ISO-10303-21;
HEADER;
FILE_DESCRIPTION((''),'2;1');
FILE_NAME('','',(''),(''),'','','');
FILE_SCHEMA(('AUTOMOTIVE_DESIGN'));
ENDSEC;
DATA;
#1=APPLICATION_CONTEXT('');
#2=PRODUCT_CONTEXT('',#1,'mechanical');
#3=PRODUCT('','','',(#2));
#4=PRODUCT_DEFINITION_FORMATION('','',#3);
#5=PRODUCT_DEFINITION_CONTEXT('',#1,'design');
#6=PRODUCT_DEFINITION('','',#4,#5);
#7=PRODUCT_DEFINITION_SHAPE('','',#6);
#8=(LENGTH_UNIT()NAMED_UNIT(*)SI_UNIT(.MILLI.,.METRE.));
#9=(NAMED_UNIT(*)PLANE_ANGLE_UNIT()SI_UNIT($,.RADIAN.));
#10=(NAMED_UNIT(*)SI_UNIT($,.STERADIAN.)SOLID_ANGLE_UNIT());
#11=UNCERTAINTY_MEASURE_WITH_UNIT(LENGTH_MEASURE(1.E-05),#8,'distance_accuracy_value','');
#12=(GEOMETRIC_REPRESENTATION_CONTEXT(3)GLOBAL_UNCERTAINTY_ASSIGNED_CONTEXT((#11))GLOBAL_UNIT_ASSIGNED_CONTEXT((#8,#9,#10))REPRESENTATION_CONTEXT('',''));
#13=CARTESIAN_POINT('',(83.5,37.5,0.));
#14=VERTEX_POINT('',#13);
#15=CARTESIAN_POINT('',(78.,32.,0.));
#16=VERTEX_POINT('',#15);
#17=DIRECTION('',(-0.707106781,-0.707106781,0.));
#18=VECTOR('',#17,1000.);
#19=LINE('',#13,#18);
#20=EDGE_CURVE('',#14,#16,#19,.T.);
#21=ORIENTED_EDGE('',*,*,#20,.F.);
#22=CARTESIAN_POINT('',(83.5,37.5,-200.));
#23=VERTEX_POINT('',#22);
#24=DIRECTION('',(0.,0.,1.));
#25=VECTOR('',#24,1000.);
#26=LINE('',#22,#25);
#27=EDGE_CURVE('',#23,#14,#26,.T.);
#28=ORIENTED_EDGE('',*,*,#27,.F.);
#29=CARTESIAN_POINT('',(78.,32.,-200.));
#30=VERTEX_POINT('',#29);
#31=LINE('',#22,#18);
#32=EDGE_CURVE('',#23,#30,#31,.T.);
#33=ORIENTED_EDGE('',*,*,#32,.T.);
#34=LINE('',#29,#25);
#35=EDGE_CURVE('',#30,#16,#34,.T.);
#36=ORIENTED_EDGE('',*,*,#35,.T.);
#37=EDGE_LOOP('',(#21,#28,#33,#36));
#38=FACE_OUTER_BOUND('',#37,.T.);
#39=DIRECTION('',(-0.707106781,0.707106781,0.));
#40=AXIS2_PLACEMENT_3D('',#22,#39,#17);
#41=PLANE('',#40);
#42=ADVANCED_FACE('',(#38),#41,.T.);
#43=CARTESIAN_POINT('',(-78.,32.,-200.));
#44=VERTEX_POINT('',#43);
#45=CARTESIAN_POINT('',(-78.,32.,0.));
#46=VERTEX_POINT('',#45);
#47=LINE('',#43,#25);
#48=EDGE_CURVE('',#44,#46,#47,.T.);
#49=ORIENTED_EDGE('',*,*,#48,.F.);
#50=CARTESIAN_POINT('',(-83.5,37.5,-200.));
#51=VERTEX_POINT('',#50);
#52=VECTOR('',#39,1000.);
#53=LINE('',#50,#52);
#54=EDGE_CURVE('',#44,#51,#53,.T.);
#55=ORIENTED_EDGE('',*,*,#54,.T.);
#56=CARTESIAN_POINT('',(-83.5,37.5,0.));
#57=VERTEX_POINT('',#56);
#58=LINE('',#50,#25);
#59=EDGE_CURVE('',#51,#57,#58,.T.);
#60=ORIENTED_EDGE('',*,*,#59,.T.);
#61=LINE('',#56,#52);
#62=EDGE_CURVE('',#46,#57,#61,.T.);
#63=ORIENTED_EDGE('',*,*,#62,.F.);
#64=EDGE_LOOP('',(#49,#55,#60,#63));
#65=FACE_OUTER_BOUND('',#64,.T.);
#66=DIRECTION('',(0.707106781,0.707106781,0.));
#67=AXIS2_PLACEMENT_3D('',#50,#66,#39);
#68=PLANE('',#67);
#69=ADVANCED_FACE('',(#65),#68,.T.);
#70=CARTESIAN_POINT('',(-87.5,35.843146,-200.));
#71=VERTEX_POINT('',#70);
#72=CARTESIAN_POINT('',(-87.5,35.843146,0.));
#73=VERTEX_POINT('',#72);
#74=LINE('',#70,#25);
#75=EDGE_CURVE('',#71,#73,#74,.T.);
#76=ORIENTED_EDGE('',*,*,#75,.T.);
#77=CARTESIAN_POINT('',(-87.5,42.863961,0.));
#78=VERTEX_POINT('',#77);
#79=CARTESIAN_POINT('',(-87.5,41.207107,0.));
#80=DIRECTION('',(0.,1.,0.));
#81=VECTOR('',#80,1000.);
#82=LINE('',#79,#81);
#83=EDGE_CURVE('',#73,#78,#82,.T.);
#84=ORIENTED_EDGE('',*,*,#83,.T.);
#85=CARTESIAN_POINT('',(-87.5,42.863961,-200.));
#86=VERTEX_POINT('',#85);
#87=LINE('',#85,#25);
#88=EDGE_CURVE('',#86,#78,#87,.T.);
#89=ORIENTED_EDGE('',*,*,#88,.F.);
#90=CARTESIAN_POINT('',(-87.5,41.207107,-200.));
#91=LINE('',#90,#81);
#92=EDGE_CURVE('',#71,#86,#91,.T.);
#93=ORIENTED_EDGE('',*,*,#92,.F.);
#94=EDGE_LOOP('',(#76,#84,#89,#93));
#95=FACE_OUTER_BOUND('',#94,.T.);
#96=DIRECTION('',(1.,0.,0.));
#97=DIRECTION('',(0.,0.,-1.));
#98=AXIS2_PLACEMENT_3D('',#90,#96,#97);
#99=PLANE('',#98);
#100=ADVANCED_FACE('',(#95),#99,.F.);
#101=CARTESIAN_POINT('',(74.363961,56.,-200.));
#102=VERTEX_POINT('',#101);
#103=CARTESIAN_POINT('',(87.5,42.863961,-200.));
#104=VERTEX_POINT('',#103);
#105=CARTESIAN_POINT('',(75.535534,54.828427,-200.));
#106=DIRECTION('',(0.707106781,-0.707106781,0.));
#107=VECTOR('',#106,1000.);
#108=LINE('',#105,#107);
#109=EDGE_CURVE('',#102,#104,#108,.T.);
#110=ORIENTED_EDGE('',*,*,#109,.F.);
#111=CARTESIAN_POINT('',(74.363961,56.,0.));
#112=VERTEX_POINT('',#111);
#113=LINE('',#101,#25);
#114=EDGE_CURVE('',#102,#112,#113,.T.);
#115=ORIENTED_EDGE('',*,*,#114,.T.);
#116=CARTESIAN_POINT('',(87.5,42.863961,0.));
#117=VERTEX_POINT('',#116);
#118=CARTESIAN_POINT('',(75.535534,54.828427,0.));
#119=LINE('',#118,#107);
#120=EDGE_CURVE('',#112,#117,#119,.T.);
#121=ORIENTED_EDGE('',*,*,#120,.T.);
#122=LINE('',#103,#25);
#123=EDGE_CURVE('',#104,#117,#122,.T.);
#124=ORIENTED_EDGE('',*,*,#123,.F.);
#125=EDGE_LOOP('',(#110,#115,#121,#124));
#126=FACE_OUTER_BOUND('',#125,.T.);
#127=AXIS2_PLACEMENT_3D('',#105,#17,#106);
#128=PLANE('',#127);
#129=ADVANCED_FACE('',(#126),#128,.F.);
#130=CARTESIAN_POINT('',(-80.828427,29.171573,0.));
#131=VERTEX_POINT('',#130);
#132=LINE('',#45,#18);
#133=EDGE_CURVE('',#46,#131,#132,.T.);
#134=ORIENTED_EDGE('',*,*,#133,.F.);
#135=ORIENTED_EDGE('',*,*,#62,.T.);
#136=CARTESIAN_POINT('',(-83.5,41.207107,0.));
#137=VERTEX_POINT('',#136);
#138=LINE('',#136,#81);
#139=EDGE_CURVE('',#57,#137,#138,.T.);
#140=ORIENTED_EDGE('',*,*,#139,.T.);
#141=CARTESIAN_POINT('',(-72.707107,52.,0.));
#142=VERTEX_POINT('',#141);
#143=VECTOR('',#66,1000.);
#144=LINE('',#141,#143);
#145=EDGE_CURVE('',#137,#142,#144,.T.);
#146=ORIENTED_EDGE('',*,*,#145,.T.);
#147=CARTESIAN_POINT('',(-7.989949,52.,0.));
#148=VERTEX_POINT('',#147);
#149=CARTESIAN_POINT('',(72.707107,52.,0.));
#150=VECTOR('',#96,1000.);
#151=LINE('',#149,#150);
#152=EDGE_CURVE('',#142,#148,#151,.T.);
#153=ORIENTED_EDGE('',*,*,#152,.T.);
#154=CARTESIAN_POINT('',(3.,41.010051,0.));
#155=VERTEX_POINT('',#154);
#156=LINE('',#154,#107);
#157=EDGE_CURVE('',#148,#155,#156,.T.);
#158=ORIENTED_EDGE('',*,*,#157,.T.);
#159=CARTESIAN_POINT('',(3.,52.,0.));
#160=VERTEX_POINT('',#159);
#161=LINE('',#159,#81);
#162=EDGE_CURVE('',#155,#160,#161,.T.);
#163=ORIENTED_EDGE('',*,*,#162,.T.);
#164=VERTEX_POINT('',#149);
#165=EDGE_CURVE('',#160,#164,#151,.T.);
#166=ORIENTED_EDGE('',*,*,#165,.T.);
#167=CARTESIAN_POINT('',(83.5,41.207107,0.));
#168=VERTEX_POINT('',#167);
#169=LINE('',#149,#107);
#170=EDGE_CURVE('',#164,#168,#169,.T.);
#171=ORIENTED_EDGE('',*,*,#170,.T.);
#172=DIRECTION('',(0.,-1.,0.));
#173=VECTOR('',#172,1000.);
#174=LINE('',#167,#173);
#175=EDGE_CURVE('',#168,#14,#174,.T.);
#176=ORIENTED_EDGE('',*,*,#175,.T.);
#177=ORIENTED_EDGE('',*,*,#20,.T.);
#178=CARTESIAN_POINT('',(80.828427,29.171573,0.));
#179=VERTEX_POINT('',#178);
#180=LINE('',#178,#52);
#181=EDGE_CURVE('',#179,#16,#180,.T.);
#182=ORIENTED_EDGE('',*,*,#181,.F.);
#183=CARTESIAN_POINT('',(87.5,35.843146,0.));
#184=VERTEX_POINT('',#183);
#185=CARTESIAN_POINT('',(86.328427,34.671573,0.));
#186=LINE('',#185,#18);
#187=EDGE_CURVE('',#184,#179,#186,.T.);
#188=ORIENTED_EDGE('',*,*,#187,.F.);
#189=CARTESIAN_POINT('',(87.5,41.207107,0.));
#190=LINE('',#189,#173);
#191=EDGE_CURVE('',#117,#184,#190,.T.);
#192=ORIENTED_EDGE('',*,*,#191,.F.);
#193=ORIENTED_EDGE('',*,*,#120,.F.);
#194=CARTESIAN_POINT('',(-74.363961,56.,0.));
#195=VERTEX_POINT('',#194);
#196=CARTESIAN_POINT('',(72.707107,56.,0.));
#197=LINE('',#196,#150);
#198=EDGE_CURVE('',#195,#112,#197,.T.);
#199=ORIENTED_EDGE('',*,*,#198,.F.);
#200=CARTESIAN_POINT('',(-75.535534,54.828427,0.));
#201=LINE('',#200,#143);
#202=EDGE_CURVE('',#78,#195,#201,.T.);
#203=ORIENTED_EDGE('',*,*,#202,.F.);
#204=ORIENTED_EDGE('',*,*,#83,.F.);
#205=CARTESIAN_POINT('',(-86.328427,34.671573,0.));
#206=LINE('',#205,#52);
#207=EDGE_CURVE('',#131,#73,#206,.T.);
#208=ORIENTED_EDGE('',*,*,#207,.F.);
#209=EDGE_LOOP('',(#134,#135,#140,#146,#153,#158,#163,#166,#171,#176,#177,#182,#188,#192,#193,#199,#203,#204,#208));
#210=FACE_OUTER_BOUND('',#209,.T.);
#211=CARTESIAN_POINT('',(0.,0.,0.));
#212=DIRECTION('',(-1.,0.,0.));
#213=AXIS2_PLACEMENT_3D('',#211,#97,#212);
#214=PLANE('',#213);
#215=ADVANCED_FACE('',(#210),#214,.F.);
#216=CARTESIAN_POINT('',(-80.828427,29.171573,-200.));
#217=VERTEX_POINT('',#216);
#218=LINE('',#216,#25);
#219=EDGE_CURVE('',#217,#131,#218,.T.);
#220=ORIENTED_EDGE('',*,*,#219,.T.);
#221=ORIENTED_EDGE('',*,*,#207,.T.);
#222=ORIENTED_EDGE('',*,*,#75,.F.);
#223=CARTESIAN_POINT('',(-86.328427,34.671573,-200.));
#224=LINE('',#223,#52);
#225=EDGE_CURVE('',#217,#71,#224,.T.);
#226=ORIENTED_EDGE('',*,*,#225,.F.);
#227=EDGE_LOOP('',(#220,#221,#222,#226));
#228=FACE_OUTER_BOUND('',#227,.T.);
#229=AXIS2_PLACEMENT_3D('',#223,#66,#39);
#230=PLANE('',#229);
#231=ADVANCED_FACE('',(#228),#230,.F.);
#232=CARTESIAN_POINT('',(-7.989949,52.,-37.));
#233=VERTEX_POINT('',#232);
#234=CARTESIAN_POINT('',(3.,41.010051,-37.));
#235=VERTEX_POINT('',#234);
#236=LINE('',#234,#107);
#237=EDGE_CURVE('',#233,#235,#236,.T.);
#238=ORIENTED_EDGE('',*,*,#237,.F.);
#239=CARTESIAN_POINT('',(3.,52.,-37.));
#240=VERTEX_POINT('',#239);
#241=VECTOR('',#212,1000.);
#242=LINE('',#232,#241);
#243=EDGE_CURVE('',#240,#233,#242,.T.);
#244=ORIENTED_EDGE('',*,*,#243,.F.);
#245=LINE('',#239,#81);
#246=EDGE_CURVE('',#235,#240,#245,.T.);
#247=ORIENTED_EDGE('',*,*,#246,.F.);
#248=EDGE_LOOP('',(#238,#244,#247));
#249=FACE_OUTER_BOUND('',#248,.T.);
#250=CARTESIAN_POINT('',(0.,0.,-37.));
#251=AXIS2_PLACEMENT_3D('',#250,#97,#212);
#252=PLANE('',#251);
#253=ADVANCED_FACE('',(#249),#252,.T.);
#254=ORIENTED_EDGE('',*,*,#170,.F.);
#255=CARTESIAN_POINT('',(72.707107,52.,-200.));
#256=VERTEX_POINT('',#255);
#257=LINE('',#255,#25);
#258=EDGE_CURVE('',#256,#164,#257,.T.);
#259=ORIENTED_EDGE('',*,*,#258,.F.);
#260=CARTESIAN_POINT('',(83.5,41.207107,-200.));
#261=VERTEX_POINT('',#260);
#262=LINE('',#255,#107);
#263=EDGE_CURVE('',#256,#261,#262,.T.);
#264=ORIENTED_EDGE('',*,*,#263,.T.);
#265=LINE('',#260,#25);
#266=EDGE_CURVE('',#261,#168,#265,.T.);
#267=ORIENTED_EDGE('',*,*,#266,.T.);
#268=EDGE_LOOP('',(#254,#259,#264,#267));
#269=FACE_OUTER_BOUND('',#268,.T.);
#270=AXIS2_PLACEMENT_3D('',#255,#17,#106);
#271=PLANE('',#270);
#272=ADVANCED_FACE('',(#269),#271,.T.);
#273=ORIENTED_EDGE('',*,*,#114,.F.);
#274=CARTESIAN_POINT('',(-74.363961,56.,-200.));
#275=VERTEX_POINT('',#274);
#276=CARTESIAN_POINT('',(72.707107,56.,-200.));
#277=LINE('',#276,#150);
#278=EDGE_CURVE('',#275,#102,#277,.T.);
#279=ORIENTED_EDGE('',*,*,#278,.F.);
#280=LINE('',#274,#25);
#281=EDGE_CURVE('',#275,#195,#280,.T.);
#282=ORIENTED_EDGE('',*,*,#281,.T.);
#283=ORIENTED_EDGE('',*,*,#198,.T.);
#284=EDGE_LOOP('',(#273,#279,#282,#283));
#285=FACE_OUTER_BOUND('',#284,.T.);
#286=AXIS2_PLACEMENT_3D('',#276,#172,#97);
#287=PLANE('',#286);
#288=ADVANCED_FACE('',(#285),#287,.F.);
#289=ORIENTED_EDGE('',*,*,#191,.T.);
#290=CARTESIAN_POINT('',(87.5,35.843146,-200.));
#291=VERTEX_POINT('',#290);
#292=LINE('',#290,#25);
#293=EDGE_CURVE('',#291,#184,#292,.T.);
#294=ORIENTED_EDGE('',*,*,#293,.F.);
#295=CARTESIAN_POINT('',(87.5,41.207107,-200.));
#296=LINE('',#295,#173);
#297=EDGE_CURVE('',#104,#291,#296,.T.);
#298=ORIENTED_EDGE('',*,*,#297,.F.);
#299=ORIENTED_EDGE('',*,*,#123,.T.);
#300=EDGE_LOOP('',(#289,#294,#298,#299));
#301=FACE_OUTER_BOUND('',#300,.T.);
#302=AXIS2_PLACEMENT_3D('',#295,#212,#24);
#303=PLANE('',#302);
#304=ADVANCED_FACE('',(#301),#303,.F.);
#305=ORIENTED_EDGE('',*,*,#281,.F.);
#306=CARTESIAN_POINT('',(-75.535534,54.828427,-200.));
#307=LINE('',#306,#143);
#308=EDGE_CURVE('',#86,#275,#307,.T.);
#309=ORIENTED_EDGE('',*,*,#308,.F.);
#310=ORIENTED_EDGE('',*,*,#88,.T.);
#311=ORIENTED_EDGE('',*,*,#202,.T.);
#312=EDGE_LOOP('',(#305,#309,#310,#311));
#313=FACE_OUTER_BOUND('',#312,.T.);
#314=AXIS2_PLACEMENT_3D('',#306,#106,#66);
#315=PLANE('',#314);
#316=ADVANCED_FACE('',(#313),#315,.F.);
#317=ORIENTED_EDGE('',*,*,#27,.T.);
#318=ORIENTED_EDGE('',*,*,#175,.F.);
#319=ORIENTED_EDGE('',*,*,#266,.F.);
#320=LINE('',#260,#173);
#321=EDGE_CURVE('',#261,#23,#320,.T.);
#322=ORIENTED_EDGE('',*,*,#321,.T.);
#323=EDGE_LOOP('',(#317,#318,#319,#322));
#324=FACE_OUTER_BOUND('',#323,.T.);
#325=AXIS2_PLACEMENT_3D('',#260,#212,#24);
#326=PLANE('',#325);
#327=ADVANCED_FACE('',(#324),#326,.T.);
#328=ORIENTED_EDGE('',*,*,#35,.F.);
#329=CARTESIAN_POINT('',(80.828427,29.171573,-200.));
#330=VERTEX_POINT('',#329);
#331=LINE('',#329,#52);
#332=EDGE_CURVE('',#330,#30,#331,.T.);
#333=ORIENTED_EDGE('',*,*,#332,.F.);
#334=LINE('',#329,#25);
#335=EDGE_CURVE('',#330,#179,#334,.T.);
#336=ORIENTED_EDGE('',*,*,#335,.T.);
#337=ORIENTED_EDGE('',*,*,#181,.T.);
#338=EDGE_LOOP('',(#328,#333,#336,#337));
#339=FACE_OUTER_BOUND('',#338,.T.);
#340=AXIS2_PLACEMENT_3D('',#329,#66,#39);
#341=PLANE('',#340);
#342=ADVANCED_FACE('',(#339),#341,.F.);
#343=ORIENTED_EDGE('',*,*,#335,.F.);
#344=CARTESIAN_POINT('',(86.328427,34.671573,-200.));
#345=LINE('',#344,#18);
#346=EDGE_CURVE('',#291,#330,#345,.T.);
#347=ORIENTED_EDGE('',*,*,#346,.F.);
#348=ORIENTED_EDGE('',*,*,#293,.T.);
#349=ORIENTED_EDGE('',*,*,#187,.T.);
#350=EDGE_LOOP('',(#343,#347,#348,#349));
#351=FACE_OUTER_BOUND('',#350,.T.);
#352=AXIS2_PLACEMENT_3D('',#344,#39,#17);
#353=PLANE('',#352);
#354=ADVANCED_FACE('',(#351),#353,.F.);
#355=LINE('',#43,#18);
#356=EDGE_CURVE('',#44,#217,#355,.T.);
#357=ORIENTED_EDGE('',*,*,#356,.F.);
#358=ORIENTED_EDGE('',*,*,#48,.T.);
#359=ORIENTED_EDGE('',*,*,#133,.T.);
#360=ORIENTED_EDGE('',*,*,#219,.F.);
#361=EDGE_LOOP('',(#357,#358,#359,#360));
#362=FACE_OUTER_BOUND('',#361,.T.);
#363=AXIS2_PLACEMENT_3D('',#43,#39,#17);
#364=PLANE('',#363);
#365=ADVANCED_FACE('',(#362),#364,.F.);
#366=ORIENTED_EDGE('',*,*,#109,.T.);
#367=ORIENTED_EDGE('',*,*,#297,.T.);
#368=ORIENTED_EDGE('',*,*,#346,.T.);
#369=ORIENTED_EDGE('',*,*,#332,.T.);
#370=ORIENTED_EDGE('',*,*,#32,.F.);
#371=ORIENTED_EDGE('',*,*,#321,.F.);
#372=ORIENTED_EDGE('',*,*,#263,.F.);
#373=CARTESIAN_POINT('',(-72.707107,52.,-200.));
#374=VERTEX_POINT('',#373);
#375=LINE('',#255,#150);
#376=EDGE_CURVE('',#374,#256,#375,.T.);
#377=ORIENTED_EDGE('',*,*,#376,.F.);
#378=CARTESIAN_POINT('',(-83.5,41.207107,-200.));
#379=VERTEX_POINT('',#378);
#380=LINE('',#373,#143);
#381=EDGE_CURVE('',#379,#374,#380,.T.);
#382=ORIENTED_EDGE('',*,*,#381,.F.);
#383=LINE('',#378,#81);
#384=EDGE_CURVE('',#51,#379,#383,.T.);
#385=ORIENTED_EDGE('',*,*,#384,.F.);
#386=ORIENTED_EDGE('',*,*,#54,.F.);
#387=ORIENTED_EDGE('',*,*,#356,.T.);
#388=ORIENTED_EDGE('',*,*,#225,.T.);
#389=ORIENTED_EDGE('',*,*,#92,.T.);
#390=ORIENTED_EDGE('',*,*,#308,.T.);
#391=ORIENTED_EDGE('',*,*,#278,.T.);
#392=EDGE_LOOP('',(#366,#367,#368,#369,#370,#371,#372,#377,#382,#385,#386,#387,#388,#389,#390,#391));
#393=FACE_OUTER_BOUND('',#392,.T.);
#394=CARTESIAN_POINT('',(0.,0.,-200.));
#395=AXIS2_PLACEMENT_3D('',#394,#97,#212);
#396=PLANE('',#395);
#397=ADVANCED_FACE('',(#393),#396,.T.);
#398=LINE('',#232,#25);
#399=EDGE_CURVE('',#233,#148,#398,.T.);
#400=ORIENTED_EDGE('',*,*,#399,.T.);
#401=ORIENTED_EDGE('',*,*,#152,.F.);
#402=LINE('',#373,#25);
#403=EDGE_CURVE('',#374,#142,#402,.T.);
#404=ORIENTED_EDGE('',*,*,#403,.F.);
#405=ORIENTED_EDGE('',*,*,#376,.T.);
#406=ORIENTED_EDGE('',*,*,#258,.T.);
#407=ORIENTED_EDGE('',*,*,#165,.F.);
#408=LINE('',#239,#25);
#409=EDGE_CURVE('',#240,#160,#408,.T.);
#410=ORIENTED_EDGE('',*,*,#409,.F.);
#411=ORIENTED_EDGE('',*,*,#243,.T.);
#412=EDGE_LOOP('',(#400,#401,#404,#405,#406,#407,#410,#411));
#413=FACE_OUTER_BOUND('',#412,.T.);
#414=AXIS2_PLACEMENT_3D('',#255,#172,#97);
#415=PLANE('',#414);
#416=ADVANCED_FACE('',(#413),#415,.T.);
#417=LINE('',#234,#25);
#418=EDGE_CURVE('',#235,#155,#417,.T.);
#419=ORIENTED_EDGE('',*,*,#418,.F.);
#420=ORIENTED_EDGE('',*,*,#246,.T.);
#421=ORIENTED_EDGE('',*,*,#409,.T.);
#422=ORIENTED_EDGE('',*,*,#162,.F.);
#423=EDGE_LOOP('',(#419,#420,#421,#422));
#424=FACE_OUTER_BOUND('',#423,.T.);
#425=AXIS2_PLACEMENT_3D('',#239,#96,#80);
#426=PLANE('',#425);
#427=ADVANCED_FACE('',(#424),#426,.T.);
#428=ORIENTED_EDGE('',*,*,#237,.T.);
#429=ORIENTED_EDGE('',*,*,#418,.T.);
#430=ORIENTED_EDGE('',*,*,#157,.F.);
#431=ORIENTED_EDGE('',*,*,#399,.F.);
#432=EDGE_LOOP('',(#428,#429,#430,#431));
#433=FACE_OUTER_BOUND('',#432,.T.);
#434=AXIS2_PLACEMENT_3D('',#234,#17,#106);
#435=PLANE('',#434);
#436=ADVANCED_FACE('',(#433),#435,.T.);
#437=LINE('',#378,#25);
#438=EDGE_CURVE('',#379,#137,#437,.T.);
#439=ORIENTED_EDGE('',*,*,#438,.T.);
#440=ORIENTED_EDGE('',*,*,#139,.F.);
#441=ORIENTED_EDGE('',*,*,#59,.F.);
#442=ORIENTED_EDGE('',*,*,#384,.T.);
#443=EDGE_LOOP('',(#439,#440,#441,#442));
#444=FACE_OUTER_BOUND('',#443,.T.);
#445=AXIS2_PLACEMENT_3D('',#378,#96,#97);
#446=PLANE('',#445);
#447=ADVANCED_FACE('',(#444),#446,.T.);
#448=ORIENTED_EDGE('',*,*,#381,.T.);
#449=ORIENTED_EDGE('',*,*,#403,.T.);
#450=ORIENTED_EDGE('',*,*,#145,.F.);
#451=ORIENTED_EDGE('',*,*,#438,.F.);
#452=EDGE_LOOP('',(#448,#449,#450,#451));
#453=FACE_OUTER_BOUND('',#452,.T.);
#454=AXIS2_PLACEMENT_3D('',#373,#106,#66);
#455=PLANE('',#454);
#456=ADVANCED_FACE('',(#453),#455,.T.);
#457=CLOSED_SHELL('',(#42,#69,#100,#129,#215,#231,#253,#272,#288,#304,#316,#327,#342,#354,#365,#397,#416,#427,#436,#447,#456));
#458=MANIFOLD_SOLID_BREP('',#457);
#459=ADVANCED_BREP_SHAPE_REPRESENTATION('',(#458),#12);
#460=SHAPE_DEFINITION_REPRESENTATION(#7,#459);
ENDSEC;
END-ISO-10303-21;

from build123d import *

# Parameters (mm, degrees)
EXTRUDE_THIN1_DEPTH = 200
BOSS_EXTRUDE1_DEPTH = 37


with BuildPart() as part:
    # Sketch1 → Extrude-Thin1 (new body)
    with BuildSketch(Plane.XY):
        Polygon((78, 32), (83.5, 37.5), (83.5, 41.207106781), (72.707106781, 52), (-72.707106781, 52), (-83.5, 41.207106781), (-83.5, 37.5), (-78, 32), (-80.828427125, 29.171572875), (-87.5, 35.843145751), (-87.5, 42.863961031), (-74.363961031, 56), (74.363961031, 56), (87.5, 42.863961031), (87.5, 35.843145751), (80.828427125, 29.171572875), align=None)
    extrude(amount=-EXTRUDE_THIN1_DEPTH)

    # Sketch2 → Boss-Extrude1 (add)
    with BuildSketch(Plane.XY):
        Polygon((-7.989949494, 52), (3, 52), (3, 41.010050506), align=None)
    extrude(amount=-BOSS_EXTRUDE1_DEPTH)


solid = part.part
